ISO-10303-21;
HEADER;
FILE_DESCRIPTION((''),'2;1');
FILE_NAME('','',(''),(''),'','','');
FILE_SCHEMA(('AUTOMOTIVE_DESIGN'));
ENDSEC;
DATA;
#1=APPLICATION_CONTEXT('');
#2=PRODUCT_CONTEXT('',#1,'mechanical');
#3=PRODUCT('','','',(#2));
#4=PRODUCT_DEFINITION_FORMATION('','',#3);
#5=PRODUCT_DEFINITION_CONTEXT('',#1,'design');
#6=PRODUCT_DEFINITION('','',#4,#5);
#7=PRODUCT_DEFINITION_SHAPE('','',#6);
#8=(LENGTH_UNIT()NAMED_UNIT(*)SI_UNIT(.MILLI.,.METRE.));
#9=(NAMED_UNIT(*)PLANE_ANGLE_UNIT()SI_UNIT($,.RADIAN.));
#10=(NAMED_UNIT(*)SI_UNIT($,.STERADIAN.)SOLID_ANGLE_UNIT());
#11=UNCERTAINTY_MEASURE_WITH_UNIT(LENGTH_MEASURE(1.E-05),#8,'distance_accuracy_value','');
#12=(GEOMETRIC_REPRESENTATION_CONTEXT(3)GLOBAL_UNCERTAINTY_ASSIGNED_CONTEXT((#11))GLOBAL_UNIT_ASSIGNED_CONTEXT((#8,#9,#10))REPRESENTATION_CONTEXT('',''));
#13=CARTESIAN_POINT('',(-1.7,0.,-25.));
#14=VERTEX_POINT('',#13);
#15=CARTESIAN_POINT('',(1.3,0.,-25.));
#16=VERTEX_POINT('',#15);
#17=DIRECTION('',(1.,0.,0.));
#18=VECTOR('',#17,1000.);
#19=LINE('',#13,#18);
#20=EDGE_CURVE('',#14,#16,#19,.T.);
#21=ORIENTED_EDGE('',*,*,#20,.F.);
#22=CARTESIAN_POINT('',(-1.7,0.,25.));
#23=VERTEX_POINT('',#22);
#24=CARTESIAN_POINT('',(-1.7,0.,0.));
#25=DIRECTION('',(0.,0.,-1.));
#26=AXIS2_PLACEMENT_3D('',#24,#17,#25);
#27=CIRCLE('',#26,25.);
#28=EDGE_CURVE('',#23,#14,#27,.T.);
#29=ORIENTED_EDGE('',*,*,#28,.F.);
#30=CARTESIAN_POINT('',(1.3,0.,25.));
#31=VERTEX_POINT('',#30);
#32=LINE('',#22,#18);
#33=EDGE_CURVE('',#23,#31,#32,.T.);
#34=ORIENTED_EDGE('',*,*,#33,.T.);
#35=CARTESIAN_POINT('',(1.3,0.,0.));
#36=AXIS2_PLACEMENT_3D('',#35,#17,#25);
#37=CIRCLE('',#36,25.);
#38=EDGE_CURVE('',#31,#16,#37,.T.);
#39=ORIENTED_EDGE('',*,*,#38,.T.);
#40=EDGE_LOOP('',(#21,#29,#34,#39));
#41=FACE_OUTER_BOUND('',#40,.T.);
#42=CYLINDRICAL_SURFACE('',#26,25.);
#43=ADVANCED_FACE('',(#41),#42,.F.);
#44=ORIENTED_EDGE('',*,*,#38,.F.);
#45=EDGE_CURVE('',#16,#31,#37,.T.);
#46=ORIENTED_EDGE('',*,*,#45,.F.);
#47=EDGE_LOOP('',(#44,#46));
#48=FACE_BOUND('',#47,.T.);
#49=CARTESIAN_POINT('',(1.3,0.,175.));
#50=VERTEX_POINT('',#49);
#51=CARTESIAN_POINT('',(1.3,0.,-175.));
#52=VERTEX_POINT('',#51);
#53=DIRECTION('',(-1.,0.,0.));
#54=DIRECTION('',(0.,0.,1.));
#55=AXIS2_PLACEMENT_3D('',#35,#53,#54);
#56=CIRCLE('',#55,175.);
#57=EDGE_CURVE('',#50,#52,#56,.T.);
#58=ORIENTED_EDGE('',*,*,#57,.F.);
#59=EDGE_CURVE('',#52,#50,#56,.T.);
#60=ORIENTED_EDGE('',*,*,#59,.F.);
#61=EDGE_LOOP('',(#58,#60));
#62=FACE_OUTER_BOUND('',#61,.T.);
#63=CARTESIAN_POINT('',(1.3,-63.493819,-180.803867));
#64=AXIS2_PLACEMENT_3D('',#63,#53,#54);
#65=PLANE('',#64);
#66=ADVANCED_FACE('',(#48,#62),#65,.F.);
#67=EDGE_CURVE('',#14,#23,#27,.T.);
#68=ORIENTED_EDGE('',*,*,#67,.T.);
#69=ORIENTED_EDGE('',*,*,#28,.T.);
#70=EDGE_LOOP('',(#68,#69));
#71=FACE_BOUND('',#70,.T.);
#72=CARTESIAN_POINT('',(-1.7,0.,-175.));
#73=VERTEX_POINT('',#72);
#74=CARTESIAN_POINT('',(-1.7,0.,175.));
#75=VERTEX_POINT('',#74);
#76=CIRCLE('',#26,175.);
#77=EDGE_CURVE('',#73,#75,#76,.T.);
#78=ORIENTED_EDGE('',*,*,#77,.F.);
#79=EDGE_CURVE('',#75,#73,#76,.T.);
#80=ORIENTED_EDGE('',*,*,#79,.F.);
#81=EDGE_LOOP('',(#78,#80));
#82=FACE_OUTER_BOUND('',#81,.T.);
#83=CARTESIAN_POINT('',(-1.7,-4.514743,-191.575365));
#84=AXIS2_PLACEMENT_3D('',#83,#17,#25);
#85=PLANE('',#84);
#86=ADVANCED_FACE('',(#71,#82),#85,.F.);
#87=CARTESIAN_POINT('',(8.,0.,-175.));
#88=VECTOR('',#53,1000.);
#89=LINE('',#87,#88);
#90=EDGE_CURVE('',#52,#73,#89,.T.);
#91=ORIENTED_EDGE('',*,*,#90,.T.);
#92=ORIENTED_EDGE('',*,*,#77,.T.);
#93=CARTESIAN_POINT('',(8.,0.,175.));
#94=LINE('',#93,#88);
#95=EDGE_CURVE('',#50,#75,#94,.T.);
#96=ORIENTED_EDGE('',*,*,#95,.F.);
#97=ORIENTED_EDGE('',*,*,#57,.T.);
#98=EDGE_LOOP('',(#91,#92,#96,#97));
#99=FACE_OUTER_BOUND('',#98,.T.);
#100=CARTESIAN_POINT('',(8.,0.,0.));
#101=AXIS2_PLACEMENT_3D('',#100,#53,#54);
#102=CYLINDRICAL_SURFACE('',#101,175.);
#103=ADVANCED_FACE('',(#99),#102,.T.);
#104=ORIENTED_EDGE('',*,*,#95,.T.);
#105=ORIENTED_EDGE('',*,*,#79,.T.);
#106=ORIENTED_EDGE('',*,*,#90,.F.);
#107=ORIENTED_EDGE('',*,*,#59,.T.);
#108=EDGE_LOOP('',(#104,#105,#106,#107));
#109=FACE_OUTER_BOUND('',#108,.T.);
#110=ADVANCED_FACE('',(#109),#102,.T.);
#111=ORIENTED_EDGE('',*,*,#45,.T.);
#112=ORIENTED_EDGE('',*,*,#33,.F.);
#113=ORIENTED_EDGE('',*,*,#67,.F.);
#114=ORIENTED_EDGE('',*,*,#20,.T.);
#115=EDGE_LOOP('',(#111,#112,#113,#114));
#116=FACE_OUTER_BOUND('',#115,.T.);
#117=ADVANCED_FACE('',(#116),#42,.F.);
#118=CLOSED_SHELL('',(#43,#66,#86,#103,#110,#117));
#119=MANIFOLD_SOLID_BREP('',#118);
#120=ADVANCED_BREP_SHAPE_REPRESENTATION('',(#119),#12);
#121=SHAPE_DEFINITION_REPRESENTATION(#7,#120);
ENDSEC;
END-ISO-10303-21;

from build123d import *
from OCP.BRepFilletAPI import BRepFilletAPI_MakeChamfer

# Parameters (mm, degrees)
BOSS_EXTRUDE1_DEPTH = 4
CUT_EXTRUDE1_START  = -0.7
CUT_EXTRUDE1_DEPTH  = 0.7
CUT_EXTRUDE2_DEPTH  = 0.3
BOSS_EXTRUDE2_START = 0.3
BOSS_EXTRUDE2_DEPTH = 0.3
SKETCH5_W           = 3
SKETCH5_H           = 25
CHAMFER1_SIZE       = 1.130008551
CHAMFER1_SIZE2      = 0.565471506
SKETCH6_OUTSIDE_W   = 515.14
SKETCH6_OUTSIDE_H   = 515.14
SKETCH6_OUTSIDE_R   = 175
CUT_EXTRUDE3_DEPTH  = 10


with BuildPart() as part:
    # Sketch1 → Boss-Extrude1 (new body)
    with BuildSketch(Plane(origin=(-2, 0, 0), x_dir=(0, -1, 0), z_dir=(-1, 0, 0))):
        with BuildLine():
            Line((8.128598306, -199.834746453), (3.648717236, -192.075364828))
            ThreePointArc((3.648717236, -192.075364828), (3.941166203, -190.756212784), (5.280787083, -190.932577218))
            Line((5.280787083, -190.932577218), (12.558103906, -199.605345687))
            ThreePointArc((12.558103906, -199.605345687), (41.461654936, -195.655133258), (69.483089108, -187.54226278))
            Line((69.483089108, -187.54226278), (62.824688236, -181.547011706))
            ThreePointArc((62.824688236, -181.547011706), (62.695183332, -180.202051857), (64.023738106, -179.955818784))
            Line((64.023738106, -179.955818784), (73.624910537, -185.955297179))
            ThreePointArc((73.624910537, -185.955297179), (99.893138317, -173.266733442), (124.03609103, -156.891835741))
            Line((124.03609103, -156.891835741), (115.850941026, -153.247572166))
            ThreePointArc((115.850941026, -153.247572166), (115.312159093, -152.008458554), (116.499599564, -151.363730982))
            Line((116.499599564, -151.363730982), (127.48479795, -154.102648556))
            ThreePointArc((127.48479795, -154.102648556), (148.546385322, -133.917778536), (166.447576152, -110.883742691))
            Line((166.447576152, -110.883742691), (157.536896527, -109.947192524))
            ThreePointArc((157.536896527, -109.947192524), (156.641577295, -108.935218222), (157.571668516, -107.955106578))
            Line((157.571668516, -107.955106578), (168.8655851, -107.165358997))
            ThreePointArc((168.8655851, -107.165358997), (182.658877149, -81.460018407), (192.566012812, -54.021576334))
            Line((192.566012812, -54.021576334), (183.802042972, -55.88441563))
            ThreePointArc((183.802042972, -55.88441563), (182.637826525, -55.198639734), (183.219524688, -53.979084175))
            Line((183.219524688, -53.979084175), (193.716632226, -49.737977434))
            ThreePointArc((193.716632226, -49.737977434), (198.891445421, -21.028384111), (199.834746452, 8.128598305))
            Line((199.834746452, 8.128598305), (192.075364827, 3.648717235))
            ThreePointArc((192.075364827, 3.648717235), (190.756212783, 3.941166202), (190.932577217, 5.280787082))
            Line((190.932577217, 5.280787082), (199.605345686, 12.558103905))
            ThreePointArc((199.605345686, 12.558103905), (195.655133257, 41.461654935), (187.542262779, 69.483089106))
            Line((187.542262779, 69.483089106), (181.547011705, 62.824688235))
            ThreePointArc((181.547011705, 62.824688235), (180.202051856, 62.695183331), (179.955818783, 64.023738105))
            Line((179.955818783, 64.023738105), (185.955297178, 73.624910536))
            ThreePointArc((185.955297178, 73.624910536), (173.266733441, 99.893138316), (156.89183574, 124.036091029))
            Line((156.89183574, 124.036091029), (153.247572165, 115.850941024))
            ThreePointArc((153.247572165, 115.850941024), (152.008458553, 115.312159092), (151.363730981, 116.499599563))
            Line((151.363730981, 116.499599563), (154.102648555, 127.484797949))
            ThreePointArc((154.102648555, 127.484797949), (133.917778535, 148.546385321), (110.88374269, 166.447576151))
            Line((110.88374269, 166.447576151), (109.947192523, 157.536896526))
            ThreePointArc((109.947192523, 157.536896526), (108.935218221, 156.641577294), (107.955106577, 157.571668515))
            Line((107.955106577, 157.571668515), (107.165358996, 168.865585099))
            ThreePointArc((107.165358996, 168.865585099), (81.460018406, 182.658877148), (54.021576333, 192.566012811))
            Line((54.021576333, 192.566012811), (55.884415629, 183.802042971))
            ThreePointArc((55.884415629, 183.802042971), (55.198639733, 182.637826524), (53.979084174, 183.219524687))
            Line((53.979084174, 183.219524687), (49.737977433, 193.716632225))
            ThreePointArc((49.737977433, 193.716632225), (21.02838411, 198.89144542), (-8.128598306, 199.834746451))
            Line((-8.128598306, 199.834746451), (-3.648717236, 192.075364826))
            ThreePointArc((-3.648717236, 192.075364826), (-3.941166203, 190.756212782), (-5.280787083, 190.932577216))
            Line((-5.280787083, 190.932577216), (-12.558103906, 199.605345685))
            ThreePointArc((-12.558103906, 199.605345685), (-41.461654936, 195.655133256), (-69.483089107, 187.542262777))
            Line((-69.483089107, 187.542262777), (-62.824688236, 181.547011704))
            ThreePointArc((-62.824688236, 181.547011704), (-62.695183332, 180.202051855), (-64.023738106, 179.955818782))
            Line((-64.023738106, 179.955818782), (-73.624910537, 185.955297177))
            ThreePointArc((-73.624910537, 185.955297177), (-99.893138317, 173.26673344), (-124.03609103, 156.891835739))
            Line((-124.03609103, 156.891835739), (-115.850941025, 153.247572164))
            ThreePointArc((-115.850941025, 153.247572164), (-115.312159093, 152.008458552), (-116.499599564, 151.36373098))
            Line((-116.499599564, 151.36373098), (-127.48479795, 154.102648554))
            ThreePointArc((-127.48479795, 154.102648554), (-148.546385322, 133.917778533), (-166.447576152, 110.883742689))
            Line((-166.447576152, 110.883742689), (-157.536896527, 109.947192521))
            ThreePointArc((-157.536896527, 109.947192521), (-156.641577295, 108.93521822), (-157.571668516, 107.955106576))
            Line((-157.571668516, 107.955106576), (-168.8655851, 107.165358995))
            ThreePointArc((-168.8655851, 107.165358995), (-182.658877149, 81.460018404), (-192.566012812, 54.021576332))
            Line((-192.566012812, 54.021576332), (-183.802042972, 55.884415628))
            ThreePointArc((-183.802042972, 55.884415628), (-182.637826525, 55.198639732), (-183.219524688, 53.979084173))
            Line((-183.219524688, 53.979084173), (-193.716632226, 49.737977432))
            ThreePointArc((-193.716632226, 49.737977432), (-198.891445421, 21.028384109), (-199.834746452, -8.128598306))
            Line((-199.834746452, -8.128598306), (-192.075364827, -3.648717236))
            ThreePointArc((-192.075364827, -3.648717236), (-190.756212783, -3.941166203), (-190.932577217, -5.280787083))
            Line((-190.932577217, -5.280787083), (-199.605345686, -12.558103906))
            ThreePointArc((-199.605345686, -12.558103906), (-195.655133257, -41.461654937), (-187.542262778, -69.483089109))
            Line((-187.542262778, -69.483089109), (-181.547011705, -62.824688237))
            ThreePointArc((-181.547011705, -62.824688237), (-180.202051856, -62.695183333), (-179.955818783, -64.023738107))
            Line((-179.955818783, -64.023738107), (-185.955297178, -73.624910538))
            ThreePointArc((-185.955297178, -73.624910538), (-173.266733441, -99.893138318), (-156.89183574, -124.036091031))
            Line((-156.89183574, -124.036091031), (-153.247572165, -115.850941027))
            ThreePointArc((-153.247572165, -115.850941027), (-152.008458553, -115.312159094), (-151.363730981, -116.499599565))
            Line((-151.363730981, -116.499599565), (-154.102648555, -127.484797951))
            ThreePointArc((-154.102648555, -127.484797951), (-133.917778535, -148.546385324), (-110.88374269, -166.447576154))
            Line((-110.88374269, -166.447576154), (-109.947192522, -157.536896528))
            ThreePointArc((-109.947192522, -157.536896528), (-108.935218221, -156.641577296), (-107.955106577, -157.571668518))
            Line((-107.955106577, -157.571668518), (-107.165358996, -168.865585101))
            ThreePointArc((-107.165358996, -168.865585101), (-81.460018405, -182.65887715), (-54.021576333, -192.566012814))
            Line((-54.021576333, -192.566012814), (-55.884415629, -183.802042973))
            ThreePointArc((-55.884415629, -183.802042973), (-55.198639733, -182.637826526), (-53.979084174, -183.219524689))
            Line((-53.979084174, -183.219524689), (-49.737977433, -193.716632227))
            ThreePointArc((-49.737977433, -193.716632227), (-21.028384109, -198.891445422), (8.128598306, -199.834746453))
        make_face()
    extrude(amount=-BOSS_EXTRUDE1_DEPTH)

    # Sketch2 → Cut-Extrude1 (cut)
    with BuildSketch(Plane(origin=(2, 0, 0), x_dir=(0, 0, -1), z_dir=(1, 0, 0)).offset(CUT_EXTRUDE1_START)):
        with BuildLine():
            Line((181.547011705, -62.824688235), (181.845022607, -63.155662872))
            ThreePointArc((181.845022607, -63.155662872), (189.249413072, -35.226547542), (192.390100219, -6.503794095))
            Line((192.390100219, -6.503794095), (190.932577217, -5.280787082))
            ThreePointArc((190.932577217, -5.280787082), (190.756212783, -3.941166202), (192.075364827, -3.648717235))
            Line((192.075364827, -3.648717235), (192.461066825, -3.871402387))
            ThreePointArc((192.461066825, -3.871402387), (190.872489351, 24.978847229), (184.983641388, 53.266334763))
            Line((184.983641388, 53.266334763), (183.219524688, 53.979084175))
            ThreePointArc((183.219524688, 53.979084175), (182.637826525, 55.198639734), (183.802042972, 55.88441563))
            Line((183.802042972, 55.88441563), (184.237680867, 55.791817937))
            ThreePointArc((184.237680867, 55.791817937), (173.811636486, 82.739138395), (159.469694881, 107.822383645))
            Line((159.469694881, 107.822383645), (157.571668516, 107.955106578))
            ThreePointArc((157.571668516, 107.955106578), (156.641577295, 108.935218222), (157.536896527, 109.947192524))
            Line((157.536896527, 109.947192524), (157.979827047, 109.993746397))
            ThreePointArc((157.979827047, 109.993746397), (139.736889624, 132.400346217), (118.345743548, 151.824026374))
            Line((118.345743548, 151.824026374), (116.499599564, 151.363730982))
            ThreePointArc((116.499599564, 151.363730982), (115.312159093, 152.008458554), (115.850941025, 153.247572166))
            Line((115.850941025, 153.247572166), (116.257807045, 153.428720589))
            ThreePointArc((116.257807045, 153.428720589), (91.983722402, 169.101285665), (65.637286273, 180.964075582))
            Line((65.637286273, 180.964075582), (64.023738106, 179.955818784))
            ThreePointArc((64.023738106, 179.955818784), (62.695183332, 180.202051857), (62.824688236, 181.547011706))
            Line((62.824688236, 181.547011706), (63.155662873, 181.845022608))
            ThreePointArc((63.155662873, 181.845022608), (35.226547543, 189.249413073), (6.503794096, 192.39010022))
            Line((6.503794096, 192.39010022), (5.280787083, 190.932577218))
            ThreePointArc((5.280787083, 190.932577218), (3.941166203, 190.756212784), (3.648717236, 192.075364828))
            Line((3.648717236, 192.075364828), (3.871402389, 192.461066826))
            ThreePointArc((3.871402389, 192.461066826), (-24.978847228, 190.872489352), (-53.266334761, 184.983641389))
            Line((-53.266334761, 184.983641389), (-53.979084174, 183.219524689))
            ThreePointArc((-53.979084174, 183.219524689), (-55.198639733, 182.637826526), (-55.884415629, 183.802042973))
            Line((-55.884415629, 183.802042973), (-55.791817936, 184.237680869))
            ThreePointArc((-55.791817936, 184.237680869), (-82.739138394, 173.811636487), (-107.822383644, 159.469694882))
            Line((-107.822383644, 159.469694882), (-107.955106577, 157.571668518))
            ThreePointArc((-107.955106577, 157.571668518), (-108.935218221, 156.641577296), (-109.947192522, 157.536896528))
            Line((-109.947192522, 157.536896528), (-109.993746396, 157.979827048))
            ThreePointArc((-109.993746396, 157.979827048), (-132.400346216, 139.736889625), (-151.824026373, 118.345743549))
            Line((-151.824026373, 118.345743549), (-151.363730981, 116.499599565))
            ThreePointArc((-151.363730981, 116.499599565), (-152.008458553, 115.312159094), (-153.247572165, 115.850941027))
            Line((-153.247572165, 115.850941027), (-153.428720588, 116.257807046))
            ThreePointArc((-153.428720588, 116.257807046), (-169.101285664, 91.983722403), (-180.96407558, 65.637286274))
            Line((-180.96407558, 65.637286274), (-179.955818783, 64.023738107))
            ThreePointArc((-179.955818783, 64.023738107), (-180.202051856, 62.695183333), (-181.547011705, 62.824688237))
            Line((-181.547011705, 62.824688237), (-181.845022607, 63.155662874))
            ThreePointArc((-181.845022607, 63.155662874), (-189.249413072, 35.226547543), (-192.390100219, 6.503794096))
            Line((-192.390100219, 6.503794096), (-190.932577217, 5.280787083))
            ThreePointArc((-190.932577217, 5.280787083), (-190.756212783, 3.941166203), (-192.075364827, 3.648717236))
            Line((-192.075364827, 3.648717236), (-192.461066825, 3.871402388))
            ThreePointArc((-192.461066825, 3.871402388), (-190.872489351, -24.978847227), (-184.983641388, -53.26633476))
            Line((-184.983641388, -53.26633476), (-183.219524688, -53.979084173))
            ThreePointArc((-183.219524688, -53.979084173), (-182.637826525, -55.198639732), (-183.802042972, -55.884415628))
            Line((-183.802042972, -55.884415628), (-184.237680867, -55.791817935))
            ThreePointArc((-184.237680867, -55.791817935), (-173.811636486, -82.739138393), (-159.46969488, -107.822383643))
            Line((-159.46969488, -107.822383643), (-157.571668516, -107.955106576))
            ThreePointArc((-157.571668516, -107.955106576), (-156.641577295, -108.93521822), (-157.536896527, -109.947192521))
            Line((-157.536896527, -109.947192521), (-157.979827047, -109.993746395))
            ThreePointArc((-157.979827047, -109.993746395), (-139.736889624, -132.400346215), (-118.345743548, -151.824026372))
            Line((-118.345743548, -151.824026372), (-116.499599564, -151.36373098))
            ThreePointArc((-116.499599564, -151.36373098), (-115.312159093, -152.008458552), (-115.850941025, -153.247572164))
            Line((-115.850941025, -153.247572164), (-116.257807045, -153.428720587))
            ThreePointArc((-116.257807045, -153.428720587), (-91.983722402, -169.101285663), (-65.637286273, -180.964075579))
            Line((-65.637286273, -180.964075579), (-64.023738106, -179.955818782))
            ThreePointArc((-64.023738106, -179.955818782), (-62.695183332, -180.202051855), (-62.824688236, -181.547011704))
            Line((-62.824688236, -181.547011704), (-63.155662873, -181.845022606))
            ThreePointArc((-63.155662873, -181.845022606), (-35.226547543, -189.249413071), (-6.503794096, -192.390100218))
            Line((-6.503794096, -192.390100218), (-5.280787083, -190.932577216))
            ThreePointArc((-5.280787083, -190.932577216), (-3.941166203, -190.756212782), (-3.648717236, -192.075364826))
            Line((-3.648717236, -192.075364826), (-3.871402388, -192.461066824))
            ThreePointArc((-3.871402388, -192.461066824), (24.978847228, -190.87248935), (53.266334762, -184.983641387))
            Line((53.266334762, -184.983641387), (53.979084174, -183.219524687))
            ThreePointArc((53.979084174, -183.219524687), (55.198639733, -182.637826524), (55.884415629, -183.802042971))
            Line((55.884415629, -183.802042971), (55.791817936, -184.237680866))
            ThreePointArc((55.791817936, -184.237680866), (82.739138394, -173.811636485), (107.822383644, -159.469694879))
            Line((107.822383644, -159.469694879), (107.955106577, -157.571668515))
            ThreePointArc((107.955106577, -157.571668515), (108.935218221, -156.641577294), (109.947192523, -157.536896526))
            Line((109.947192523, -157.536896526), (109.993746396, -157.979827046))
            ThreePointArc((109.993746396, -157.979827046), (132.400346216, -139.736889623), (151.824026373, -118.345743546))
            Line((151.824026373, -118.345743546), (151.363730981, -116.499599563))
            ThreePointArc((151.363730981, -116.499599563), (152.008458553, -115.312159092), (153.247572165, -115.850941024))
            Line((153.247572165, -115.850941024), (153.428720588, -116.257807044))
            ThreePointArc((153.428720588, -116.257807044), (169.101285664, -91.983722401), (180.964075581, -65.637286272))
            Line((180.964075581, -65.637286272), (179.955818783, -64.023738105))
            ThreePointArc((179.955818783, -64.023738105), (180.202051856, -62.695183331), (181.547011705, -62.824688235))
        make_face()
    extrude(amount=CUT_EXTRUDE1_DEPTH, mode=Mode.SUBTRACT)

    # Sketch3 → Cut-Extrude2 (cut)
    with BuildSketch(Plane.ZY.offset(2)):
        with BuildLine():
            Line((-190.932577217, -5.280787083), (-199.605345686, -12.558103906))
            ThreePointArc((-199.605345686, -12.558103906), (-195.655133257, -41.461654936), (-187.542262779, -69.483089108))
            Line((-187.542262779, -69.483089108), (-181.547011705, -62.824688236))
            ThreePointArc((-181.547011705, -62.824688236), (-180.202051856, -62.695183332), (-179.955818783, -64.023738106))
            Line((-179.955818783, -64.023738106), (-180.964075581, -65.637286273))
            ThreePointArc((-180.964075581, -65.637286273), (-169.101285664, -91.983722402), (-153.428720588, -116.257807045))
            Line((-153.428720588, -116.257807045), (-153.247572165, -115.850941025))
            ThreePointArc((-153.247572165, -115.850941025), (-152.008458553, -115.312159093), (-151.363730981, -116.499599564))
            Line((-151.363730981, -116.499599564), (-151.824026373, -118.345743548))
            ThreePointArc((-151.824026373, -118.345743548), (-132.400346216, -139.736889624), (-109.993746396, -157.979827047))
            Line((-109.993746396, -157.979827047), (-109.947192522, -157.536896527))
            ThreePointArc((-109.947192522, -157.536896527), (-108.935218221, -156.641577295), (-107.955106577, -157.571668516))
            Line((-107.955106577, -157.571668516), (-107.822383644, -159.46969488))
            ThreePointArc((-107.822383644, -159.46969488), (-82.739138394, -173.811636486), (-55.791817936, -184.237680867))
            Line((-55.791817936, -184.237680867), (-55.884415629, -183.802042972))
            ThreePointArc((-55.884415629, -183.802042972), (-55.198639733, -182.637826525), (-53.979084174, -183.219524688))
            Line((-53.979084174, -183.219524688), (-53.266334761, -184.983641388))
            ThreePointArc((-53.266334761, -184.983641388), (-24.978847228, -190.872489351), (3.871402388, -192.461066825))
            Line((3.871402388, -192.461066825), (3.648717236, -192.075364827))
            ThreePointArc((3.648717236, -192.075364827), (3.941166203, -190.756212783), (5.280787083, -190.932577217))
            Line((5.280787083, -190.932577217), (6.503794096, -192.390100219))
            ThreePointArc((6.503794096, -192.390100219), (35.226547543, -189.249413072), (63.155662873, -181.845022607))
            Line((63.155662873, -181.845022607), (62.824688236, -181.547011705))
            ThreePointArc((62.824688236, -181.547011705), (62.695183332, -180.202051856), (64.023738106, -179.955818783))
            Line((64.023738106, -179.955818783), (65.637286273, -180.964075581))
            ThreePointArc((65.637286273, -180.964075581), (91.983722402, -169.101285664), (116.257807045, -153.428720588))
            Line((116.257807045, -153.428720588), (115.850941025, -153.247572165))
            ThreePointArc((115.850941025, -153.247572165), (115.312159093, -152.008458553), (116.499599564, -151.363730981))
            Line((116.499599564, -151.363730981), (118.345743548, -151.824026373))
            ThreePointArc((118.345743548, -151.824026373), (139.736889624, -132.400346216), (157.979827047, -109.993746396))
            Line((157.979827047, -109.993746396), (157.536896527, -109.947192522))
            ThreePointArc((157.536896527, -109.947192522), (156.641577295, -108.935218221), (157.571668516, -107.955106577))
            Line((157.571668516, -107.955106577), (159.46969488, -107.822383644))
            ThreePointArc((159.46969488, -107.822383644), (173.811636486, -82.739138394), (184.237680867, -55.791817936))
            Line((184.237680867, -55.791817936), (183.802042972, -55.884415629))
            ThreePointArc((183.802042972, -55.884415629), (182.637826525, -55.198639733), (183.219524688, -53.979084174))
            Line((183.219524688, -53.979084174), (184.983641388, -53.266334761))
            ThreePointArc((184.983641388, -53.266334761), (190.872489351, -24.978847228), (192.461066825, 3.871402388))
            Line((192.461066825, 3.871402388), (192.075364827, 3.648717236))
            ThreePointArc((192.075364827, 3.648717236), (190.756212783, 3.941166203), (190.932577217, 5.280787083))
            Line((190.932577217, 5.280787083), (192.390100219, 6.503794096))
            ThreePointArc((192.390100219, 6.503794096), (189.249413072, 35.226547543), (181.845022607, 63.155662873))
            Line((181.845022607, 63.155662873), (181.547011705, 62.824688236))
            ThreePointArc((181.547011705, 62.824688236), (180.202051856, 62.695183332), (179.955818783, 64.023738106))
            Line((179.955818783, 64.023738106), (180.964075581, 65.637286273))
            ThreePointArc((180.964075581, 65.637286273), (169.101285664, 91.983722402), (153.428720588, 116.257807045))
            Line((153.428720588, 116.257807045), (153.247572165, 115.850941025))
            ThreePointArc((153.247572165, 115.850941025), (152.008458553, 115.312159093), (151.363730981, 116.499599564))
            Line((151.363730981, 116.499599564), (151.824026373, 118.345743548))
            ThreePointArc((151.824026373, 118.345743548), (132.400346216, 139.736889624), (109.993746396, 157.979827047))
            Line((109.993746396, 157.979827047), (109.947192522, 157.536896527))
            ThreePointArc((109.947192522, 157.536896527), (108.935218221, 156.641577295), (107.955106577, 157.571668516))
            Line((107.955106577, 157.571668516), (107.822383644, 159.46969488))
            ThreePointArc((107.822383644, 159.46969488), (82.739138394, 173.811636486), (55.791817936, 184.237680867))
            Line((55.791817936, 184.237680867), (55.884415629, 183.802042972))
            ThreePointArc((55.884415629, 183.802042972), (55.198639733, 182.637826525), (53.979084174, 183.219524688))
            Line((53.979084174, 183.219524688), (53.266334761, 184.983641388))
            ThreePointArc((53.266334761, 184.983641388), (24.978847228, 190.872489351), (-3.871402388, 192.461066825))
            Line((-3.871402388, 192.461066825), (-3.648717236, 192.075364827))
            ThreePointArc((-3.648717236, 192.075364827), (-3.941166203, 190.756212783), (-5.280787083, 190.932577217))
            Line((-5.280787083, 190.932577217), (-6.503794096, 192.390100219))
            ThreePointArc((-6.503794096, 192.390100219), (-35.226547543, 189.249413072), (-63.155662873, 181.845022607))
            Line((-63.155662873, 181.845022607), (-62.824688236, 181.547011705))
            ThreePointArc((-62.824688236, 181.547011705), (-62.695183332, 180.202051856), (-64.023738106, 179.955818783))
            Line((-64.023738106, 179.955818783), (-65.637286273, 180.964075581))
            ThreePointArc((-65.637286273, 180.964075581), (-91.983722402, 169.101285664), (-116.257807045, 153.428720588))
            Line((-116.257807045, 153.428720588), (-115.850941025, 153.247572165))
            ThreePointArc((-115.850941025, 153.247572165), (-115.312159093, 152.008458553), (-116.499599564, 151.363730981))
            Line((-116.499599564, 151.363730981), (-118.345743548, 151.824026373))
            ThreePointArc((-118.345743548, 151.824026373), (-139.736889624, 132.400346216), (-157.979827047, 109.993746396))
            Line((-157.979827047, 109.993746396), (-157.536896527, 109.947192522))
            ThreePointArc((-157.536896527, 109.947192522), (-156.641577295, 108.935218221), (-157.571668516, 107.955106577))
            Line((-157.571668516, 107.955106577), (-159.46969488, 107.822383644))
            ThreePointArc((-159.46969488, 107.822383644), (-173.811636486, 82.739138394), (-184.237680867, 55.791817936))
            Line((-184.237680867, 55.791817936), (-183.802042972, 55.884415629))
            ThreePointArc((-183.802042972, 55.884415629), (-182.637826525, 55.198639733), (-183.219524688, 53.979084174))
            Line((-183.219524688, 53.979084174), (-184.983641388, 53.266334761))
            ThreePointArc((-184.983641388, 53.266334761), (-190.872489351, 24.978847228), (-192.461066825, -3.871402388))
            Line((-192.461066825, -3.871402388), (-192.075364827, -3.648717236))
            ThreePointArc((-192.075364827, -3.648717236), (-190.756212783, -3.941166203), (-190.932577217, -5.280787083))
        make_face()
    extrude(amount=-CUT_EXTRUDE2_DEPTH, mode=Mode.SUBTRACT)

    # Sketch4 → Boss-Extrude2 (add)
    with BuildSketch(Plane.ZY.offset(1.7).offset(BOSS_EXTRUDE2_START)):
        with BuildLine():
            Line((-199.605345686, -12.558103906), (-192.390100219, -6.503794096))
            ThreePointArc((-192.390100219, -6.503794096), (-189.249413072, -35.226547543), (-181.845022607, -63.155662873))
            Line((-181.845022607, -63.155662873), (-187.542262779, -69.483089108))
            ThreePointArc((-187.542262779, -69.483089108), (-195.655133257, -41.461654936), (-199.605345686, -12.558103906))
        make_face()
    extrude(amount=-BOSS_EXTRUDE2_DEPTH)

    # Sketch5 → Cut-Revolve1 (revolve, cut)
    with BuildSketch(Plane.XY, mode=Mode.PRIVATE) as cut_revolve1_sk:
        with Locations((-0.2, 12.5)):
            Rectangle(SKETCH5_W, SKETCH5_H)
    revolve(cut_revolve1_sk.sketch.rotate(Axis((-1.7, 0, 0), (1, 0, 0)), 270), axis=Axis((-1.7, 0, 0), (1, 0, 0)), mode=Mode.SUBTRACT)

    # Chamfer1: one chamfer whose edges measure the first distance from different faces: ONE call of the kernel's chamfer builder (chamfer() names one face for all edges)
    chamfer1_edges_1 = [part.edges().sort_by_distance(p)[0] for p in [
        (0, 54.021576333, -192.566012814),
    ]]
    chamfer1_side_1 = [part.faces().sort_by_distance(p)[0] for p in [
        (-0.007549997, 54.941858215, -188.236426965),
    ]]
    chamfer1_edges_2 = [part.edges().sort_by_distance(p)[0] for p in [
        (0, 110.88374269, -166.447576154),
    ]]
    chamfer1_side_2 = [part.faces().sort_by_distance(p)[0] for p in [
        (-0.007549998, 110.421067164, -162.045512578),
    ]]
    chamfer1_edges_3 = [part.edges().sort_by_distance(p)[0] for p in [
        (0, 156.89183574, -124.036091031),
    ]]
    chamfer1_side_3 = [part.faces().sort_by_distance(p)[0] for p in [
        (-0.007549998, 155.091492712, -119.992454383),
    ]]
    chamfer1_edges_4 = [part.edges().sort_by_distance(p)[0] for p in [
        (0, 187.542262778, -69.483089109),
    ]]
    chamfer1_side_4 = [part.faces().sort_by_distance(p)[0] for p in [
        (-0.007549998, 184.580482366, -66.193698716),
    ]]
    chamfer1_edges_5 = [part.edges().sort_by_distance(p)[0] for p in [
        (0, 199.834746452, -8.128598306),
    ]]
    chamfer1_side_5 = [part.faces().sort_by_distance(p)[0] for p in [
        (-0.007549998, 196.001448359, -5.91544262),
    ]]
    chamfer1_edges_6 = [part.edges().sort_by_distance(p)[0] for p in [
        (0, 192.566012812, 54.021576332),
    ]]
    chamfer1_side_6 = [part.faces().sort_by_distance(p)[0] for p in [
        (-0.007549998, 188.236426964, 54.941858214),
    ]]
    chamfer1_edges_7 = [part.edges().sort_by_distance(p)[0] for p in [
        (0, 166.447576152, 110.883742689),
    ]]
    chamfer1_side_7 = [part.faces().sort_by_distance(p)[0] for p in [
        (-0.007549998, 162.045512577, 110.421067163),
    ]]
    chamfer1_edges_8 = [part.edges().sort_by_distance(p)[0] for p in [
        (0, 124.03609103, 156.891835739),
    ]]
    chamfer1_side_8 = [part.faces().sort_by_distance(p)[0] for p in [
        (-0.007549998, 119.992454382, 155.091492711),
    ]]
    chamfer1_edges_9 = [part.edges().sort_by_distance(p)[0] for p in [
        (0, 69.483089107, 187.542262777),
    ]]
    chamfer1_side_9 = [part.faces().sort_by_distance(p)[0] for p in [
        (-0.007549998, 66.193698715, 184.580482365),
    ]]
    chamfer1_edges_10 = [part.edges().sort_by_distance(p)[0] for p in [
        (0, 8.128598306, 199.834746451),
    ]]
    chamfer1_side_10 = [part.faces().sort_by_distance(p)[0] for p in [
        (-0.007549998, 5.91544262, 196.001448358),
    ]]
    chamfer1_edges_11 = [part.edges().sort_by_distance(p)[0] for p in [
        (0, -54.021576333, 192.566012811),
    ]]
    chamfer1_side_11 = [part.faces().sort_by_distance(p)[0] for p in [
        (-0.007549998, -54.941858215, 188.236426963),
    ]]
    chamfer1_edges_12 = [part.edges().sort_by_distance(p)[0] for p in [
        (0, -110.88374269, 166.447576151),
    ]]
    chamfer1_side_12 = [part.faces().sort_by_distance(p)[0] for p in [
        (-0.007549998, -110.421067165, 162.045512576),
    ]]
    chamfer1_edges_13 = [part.edges().sort_by_distance(p)[0] for p in [
        (0, -156.89183574, 124.036091029),
    ]]
    chamfer1_side_13 = [part.faces().sort_by_distance(p)[0] for p in [
        (-0.007549998, -155.091492712, 119.992454381),
    ]]
    chamfer1_edges_14 = [part.edges().sort_by_distance(p)[0] for p in [
        (0, -187.542262779, 69.483089106),
    ]]
    chamfer1_side_14 = [part.faces().sort_by_distance(p)[0] for p in [
        (-0.007549998, -184.580482366, 66.193698714),
    ]]
    chamfer1_edges_15 = [part.edges().sort_by_distance(p)[0] for p in [
        (0, -199.834746452, 8.128598305),
    ]]
    chamfer1_side_15 = [part.faces().sort_by_distance(p)[0] for p in [
        (-0.007549997, -196.001448359, 5.915442619),
    ]]
    chamfer1_edges_16 = [part.edges().sort_by_distance(p)[0] for p in [
        (0, -192.566012812, -54.021576334),
    ]]
    chamfer1_side_16 = [part.faces().sort_by_distance(p)[0] for p in [
        (-0.007549997, -188.236426964, -54.941858216),
    ]]
    chamfer1_edges_17 = [part.edges().sort_by_distance(p)[0] for p in [
        (0, -166.447576152, -110.883742691),
    ]]
    chamfer1_side_17 = [part.faces().sort_by_distance(p)[0] for p in [
        (-0.007549997, -162.045512577, -110.421067166),
    ]]
    chamfer1_edges_18 = [part.edges().sort_by_distance(p)[0] for p in [
        (0, -124.03609103, -156.891835741),
    ]]
    chamfer1_side_18 = [part.faces().sort_by_distance(p)[0] for p in [
        (-0.007549997, -119.992454382, -155.091492713),
    ]]
    chamfer1_edges_19 = [part.edges().sort_by_distance(p)[0] for p in [
        (0.15, -69.483089108, -187.54226278),
    ]]
    chamfer1_side_19 = [part.faces().sort_by_distance(p)[0] for p in [
        (-0.007549997, -66.193698715, -184.580482367),
    ]]
    chamfer1_edges_20 = [part.edges().sort_by_distance(p)[0] for p in [
        (0, -8.128598306, -199.834746453),
    ]]
    chamfer1_side_20 = [part.faces().sort_by_distance(p)[0] for p in [
        (-0.007549997, -5.91544262, -196.00144836),
    ]]
    chamfer1 = BRepFilletAPI_MakeChamfer(part.part.solid().wrapped)
    for e in chamfer1_edges_1:
        chamfer1.Add(CHAMFER1_SIZE, CHAMFER1_SIZE2, e.wrapped, chamfer1_side_1[0].wrapped)  # the first distance lies on this face
    for e in chamfer1_edges_2:
        chamfer1.Add(CHAMFER1_SIZE, CHAMFER1_SIZE2, e.wrapped, chamfer1_side_2[0].wrapped)  # the first distance lies on this face
    for e in chamfer1_edges_3:
        chamfer1.Add(CHAMFER1_SIZE, CHAMFER1_SIZE2, e.wrapped, chamfer1_side_3[0].wrapped)  # the first distance lies on this face
    for e in chamfer1_edges_4:
        chamfer1.Add(CHAMFER1_SIZE, CHAMFER1_SIZE2, e.wrapped, chamfer1_side_4[0].wrapped)  # the first distance lies on this face
    for e in chamfer1_edges_5:
        chamfer1.Add(CHAMFER1_SIZE, CHAMFER1_SIZE2, e.wrapped, chamfer1_side_5[0].wrapped)  # the first distance lies on this face
    for e in chamfer1_edges_6:
        chamfer1.Add(CHAMFER1_SIZE, CHAMFER1_SIZE2, e.wrapped, chamfer1_side_6[0].wrapped)  # the first distance lies on this face
    for e in chamfer1_edges_7:
        chamfer1.Add(CHAMFER1_SIZE, CHAMFER1_SIZE2, e.wrapped, chamfer1_side_7[0].wrapped)  # the first distance lies on this face
    for e in chamfer1_edges_8:
        chamfer1.Add(CHAMFER1_SIZE, CHAMFER1_SIZE2, e.wrapped, chamfer1_side_8[0].wrapped)  # the first distance lies on this face
    for e in chamfer1_edges_9:
        chamfer1.Add(CHAMFER1_SIZE, CHAMFER1_SIZE2, e.wrapped, chamfer1_side_9[0].wrapped)  # the first distance lies on this face
    for e in chamfer1_edges_10:
        chamfer1.Add(CHAMFER1_SIZE, CHAMFER1_SIZE2, e.wrapped, chamfer1_side_10[0].wrapped)  # the first distance lies on this face
    for e in chamfer1_edges_11:
        chamfer1.Add(CHAMFER1_SIZE, CHAMFER1_SIZE2, e.wrapped, chamfer1_side_11[0].wrapped)  # the first distance lies on this face
    for e in chamfer1_edges_12:
        chamfer1.Add(CHAMFER1_SIZE, CHAMFER1_SIZE2, e.wrapped, chamfer1_side_12[0].wrapped)  # the first distance lies on this face
    for e in chamfer1_edges_13:
        chamfer1.Add(CHAMFER1_SIZE, CHAMFER1_SIZE2, e.wrapped, chamfer1_side_13[0].wrapped)  # the first distance lies on this face
    for e in chamfer1_edges_14:
        chamfer1.Add(CHAMFER1_SIZE, CHAMFER1_SIZE2, e.wrapped, chamfer1_side_14[0].wrapped)  # the first distance lies on this face
    for e in chamfer1_edges_15:
        chamfer1.Add(CHAMFER1_SIZE, CHAMFER1_SIZE2, e.wrapped, chamfer1_side_15[0].wrapped)  # the first distance lies on this face
    for e in chamfer1_edges_16:
        chamfer1.Add(CHAMFER1_SIZE, CHAMFER1_SIZE2, e.wrapped, chamfer1_side_16[0].wrapped)  # the first distance lies on this face
    for e in chamfer1_edges_17:
        chamfer1.Add(CHAMFER1_SIZE, CHAMFER1_SIZE2, e.wrapped, chamfer1_side_17[0].wrapped)  # the first distance lies on this face
    for e in chamfer1_edges_18:
        chamfer1.Add(CHAMFER1_SIZE, CHAMFER1_SIZE2, e.wrapped, chamfer1_side_18[0].wrapped)  # the first distance lies on this face
    for e in chamfer1_edges_19:
        chamfer1.Add(CHAMFER1_SIZE, CHAMFER1_SIZE2, e.wrapped, chamfer1_side_19[0].wrapped)  # the first distance lies on this face
    for e in chamfer1_edges_20:
        chamfer1.Add(CHAMFER1_SIZE, CHAMFER1_SIZE2, e.wrapped, chamfer1_side_20[0].wrapped)  # the first distance lies on this face
    add(Compound.cast(chamfer1.Shape()), mode=Mode.REPLACE)

    # Sketch6 outside → Cut-Extrude3 (cut)
    with BuildSketch(Plane.ZY.offset(2)):
        Rectangle(SKETCH6_OUTSIDE_W, SKETCH6_OUTSIDE_H)
        Circle(SKETCH6_OUTSIDE_R, mode=Mode.SUBTRACT)
    extrude(amount=-CUT_EXTRUDE3_DEPTH, mode=Mode.SUBTRACT)


solid = part.part
